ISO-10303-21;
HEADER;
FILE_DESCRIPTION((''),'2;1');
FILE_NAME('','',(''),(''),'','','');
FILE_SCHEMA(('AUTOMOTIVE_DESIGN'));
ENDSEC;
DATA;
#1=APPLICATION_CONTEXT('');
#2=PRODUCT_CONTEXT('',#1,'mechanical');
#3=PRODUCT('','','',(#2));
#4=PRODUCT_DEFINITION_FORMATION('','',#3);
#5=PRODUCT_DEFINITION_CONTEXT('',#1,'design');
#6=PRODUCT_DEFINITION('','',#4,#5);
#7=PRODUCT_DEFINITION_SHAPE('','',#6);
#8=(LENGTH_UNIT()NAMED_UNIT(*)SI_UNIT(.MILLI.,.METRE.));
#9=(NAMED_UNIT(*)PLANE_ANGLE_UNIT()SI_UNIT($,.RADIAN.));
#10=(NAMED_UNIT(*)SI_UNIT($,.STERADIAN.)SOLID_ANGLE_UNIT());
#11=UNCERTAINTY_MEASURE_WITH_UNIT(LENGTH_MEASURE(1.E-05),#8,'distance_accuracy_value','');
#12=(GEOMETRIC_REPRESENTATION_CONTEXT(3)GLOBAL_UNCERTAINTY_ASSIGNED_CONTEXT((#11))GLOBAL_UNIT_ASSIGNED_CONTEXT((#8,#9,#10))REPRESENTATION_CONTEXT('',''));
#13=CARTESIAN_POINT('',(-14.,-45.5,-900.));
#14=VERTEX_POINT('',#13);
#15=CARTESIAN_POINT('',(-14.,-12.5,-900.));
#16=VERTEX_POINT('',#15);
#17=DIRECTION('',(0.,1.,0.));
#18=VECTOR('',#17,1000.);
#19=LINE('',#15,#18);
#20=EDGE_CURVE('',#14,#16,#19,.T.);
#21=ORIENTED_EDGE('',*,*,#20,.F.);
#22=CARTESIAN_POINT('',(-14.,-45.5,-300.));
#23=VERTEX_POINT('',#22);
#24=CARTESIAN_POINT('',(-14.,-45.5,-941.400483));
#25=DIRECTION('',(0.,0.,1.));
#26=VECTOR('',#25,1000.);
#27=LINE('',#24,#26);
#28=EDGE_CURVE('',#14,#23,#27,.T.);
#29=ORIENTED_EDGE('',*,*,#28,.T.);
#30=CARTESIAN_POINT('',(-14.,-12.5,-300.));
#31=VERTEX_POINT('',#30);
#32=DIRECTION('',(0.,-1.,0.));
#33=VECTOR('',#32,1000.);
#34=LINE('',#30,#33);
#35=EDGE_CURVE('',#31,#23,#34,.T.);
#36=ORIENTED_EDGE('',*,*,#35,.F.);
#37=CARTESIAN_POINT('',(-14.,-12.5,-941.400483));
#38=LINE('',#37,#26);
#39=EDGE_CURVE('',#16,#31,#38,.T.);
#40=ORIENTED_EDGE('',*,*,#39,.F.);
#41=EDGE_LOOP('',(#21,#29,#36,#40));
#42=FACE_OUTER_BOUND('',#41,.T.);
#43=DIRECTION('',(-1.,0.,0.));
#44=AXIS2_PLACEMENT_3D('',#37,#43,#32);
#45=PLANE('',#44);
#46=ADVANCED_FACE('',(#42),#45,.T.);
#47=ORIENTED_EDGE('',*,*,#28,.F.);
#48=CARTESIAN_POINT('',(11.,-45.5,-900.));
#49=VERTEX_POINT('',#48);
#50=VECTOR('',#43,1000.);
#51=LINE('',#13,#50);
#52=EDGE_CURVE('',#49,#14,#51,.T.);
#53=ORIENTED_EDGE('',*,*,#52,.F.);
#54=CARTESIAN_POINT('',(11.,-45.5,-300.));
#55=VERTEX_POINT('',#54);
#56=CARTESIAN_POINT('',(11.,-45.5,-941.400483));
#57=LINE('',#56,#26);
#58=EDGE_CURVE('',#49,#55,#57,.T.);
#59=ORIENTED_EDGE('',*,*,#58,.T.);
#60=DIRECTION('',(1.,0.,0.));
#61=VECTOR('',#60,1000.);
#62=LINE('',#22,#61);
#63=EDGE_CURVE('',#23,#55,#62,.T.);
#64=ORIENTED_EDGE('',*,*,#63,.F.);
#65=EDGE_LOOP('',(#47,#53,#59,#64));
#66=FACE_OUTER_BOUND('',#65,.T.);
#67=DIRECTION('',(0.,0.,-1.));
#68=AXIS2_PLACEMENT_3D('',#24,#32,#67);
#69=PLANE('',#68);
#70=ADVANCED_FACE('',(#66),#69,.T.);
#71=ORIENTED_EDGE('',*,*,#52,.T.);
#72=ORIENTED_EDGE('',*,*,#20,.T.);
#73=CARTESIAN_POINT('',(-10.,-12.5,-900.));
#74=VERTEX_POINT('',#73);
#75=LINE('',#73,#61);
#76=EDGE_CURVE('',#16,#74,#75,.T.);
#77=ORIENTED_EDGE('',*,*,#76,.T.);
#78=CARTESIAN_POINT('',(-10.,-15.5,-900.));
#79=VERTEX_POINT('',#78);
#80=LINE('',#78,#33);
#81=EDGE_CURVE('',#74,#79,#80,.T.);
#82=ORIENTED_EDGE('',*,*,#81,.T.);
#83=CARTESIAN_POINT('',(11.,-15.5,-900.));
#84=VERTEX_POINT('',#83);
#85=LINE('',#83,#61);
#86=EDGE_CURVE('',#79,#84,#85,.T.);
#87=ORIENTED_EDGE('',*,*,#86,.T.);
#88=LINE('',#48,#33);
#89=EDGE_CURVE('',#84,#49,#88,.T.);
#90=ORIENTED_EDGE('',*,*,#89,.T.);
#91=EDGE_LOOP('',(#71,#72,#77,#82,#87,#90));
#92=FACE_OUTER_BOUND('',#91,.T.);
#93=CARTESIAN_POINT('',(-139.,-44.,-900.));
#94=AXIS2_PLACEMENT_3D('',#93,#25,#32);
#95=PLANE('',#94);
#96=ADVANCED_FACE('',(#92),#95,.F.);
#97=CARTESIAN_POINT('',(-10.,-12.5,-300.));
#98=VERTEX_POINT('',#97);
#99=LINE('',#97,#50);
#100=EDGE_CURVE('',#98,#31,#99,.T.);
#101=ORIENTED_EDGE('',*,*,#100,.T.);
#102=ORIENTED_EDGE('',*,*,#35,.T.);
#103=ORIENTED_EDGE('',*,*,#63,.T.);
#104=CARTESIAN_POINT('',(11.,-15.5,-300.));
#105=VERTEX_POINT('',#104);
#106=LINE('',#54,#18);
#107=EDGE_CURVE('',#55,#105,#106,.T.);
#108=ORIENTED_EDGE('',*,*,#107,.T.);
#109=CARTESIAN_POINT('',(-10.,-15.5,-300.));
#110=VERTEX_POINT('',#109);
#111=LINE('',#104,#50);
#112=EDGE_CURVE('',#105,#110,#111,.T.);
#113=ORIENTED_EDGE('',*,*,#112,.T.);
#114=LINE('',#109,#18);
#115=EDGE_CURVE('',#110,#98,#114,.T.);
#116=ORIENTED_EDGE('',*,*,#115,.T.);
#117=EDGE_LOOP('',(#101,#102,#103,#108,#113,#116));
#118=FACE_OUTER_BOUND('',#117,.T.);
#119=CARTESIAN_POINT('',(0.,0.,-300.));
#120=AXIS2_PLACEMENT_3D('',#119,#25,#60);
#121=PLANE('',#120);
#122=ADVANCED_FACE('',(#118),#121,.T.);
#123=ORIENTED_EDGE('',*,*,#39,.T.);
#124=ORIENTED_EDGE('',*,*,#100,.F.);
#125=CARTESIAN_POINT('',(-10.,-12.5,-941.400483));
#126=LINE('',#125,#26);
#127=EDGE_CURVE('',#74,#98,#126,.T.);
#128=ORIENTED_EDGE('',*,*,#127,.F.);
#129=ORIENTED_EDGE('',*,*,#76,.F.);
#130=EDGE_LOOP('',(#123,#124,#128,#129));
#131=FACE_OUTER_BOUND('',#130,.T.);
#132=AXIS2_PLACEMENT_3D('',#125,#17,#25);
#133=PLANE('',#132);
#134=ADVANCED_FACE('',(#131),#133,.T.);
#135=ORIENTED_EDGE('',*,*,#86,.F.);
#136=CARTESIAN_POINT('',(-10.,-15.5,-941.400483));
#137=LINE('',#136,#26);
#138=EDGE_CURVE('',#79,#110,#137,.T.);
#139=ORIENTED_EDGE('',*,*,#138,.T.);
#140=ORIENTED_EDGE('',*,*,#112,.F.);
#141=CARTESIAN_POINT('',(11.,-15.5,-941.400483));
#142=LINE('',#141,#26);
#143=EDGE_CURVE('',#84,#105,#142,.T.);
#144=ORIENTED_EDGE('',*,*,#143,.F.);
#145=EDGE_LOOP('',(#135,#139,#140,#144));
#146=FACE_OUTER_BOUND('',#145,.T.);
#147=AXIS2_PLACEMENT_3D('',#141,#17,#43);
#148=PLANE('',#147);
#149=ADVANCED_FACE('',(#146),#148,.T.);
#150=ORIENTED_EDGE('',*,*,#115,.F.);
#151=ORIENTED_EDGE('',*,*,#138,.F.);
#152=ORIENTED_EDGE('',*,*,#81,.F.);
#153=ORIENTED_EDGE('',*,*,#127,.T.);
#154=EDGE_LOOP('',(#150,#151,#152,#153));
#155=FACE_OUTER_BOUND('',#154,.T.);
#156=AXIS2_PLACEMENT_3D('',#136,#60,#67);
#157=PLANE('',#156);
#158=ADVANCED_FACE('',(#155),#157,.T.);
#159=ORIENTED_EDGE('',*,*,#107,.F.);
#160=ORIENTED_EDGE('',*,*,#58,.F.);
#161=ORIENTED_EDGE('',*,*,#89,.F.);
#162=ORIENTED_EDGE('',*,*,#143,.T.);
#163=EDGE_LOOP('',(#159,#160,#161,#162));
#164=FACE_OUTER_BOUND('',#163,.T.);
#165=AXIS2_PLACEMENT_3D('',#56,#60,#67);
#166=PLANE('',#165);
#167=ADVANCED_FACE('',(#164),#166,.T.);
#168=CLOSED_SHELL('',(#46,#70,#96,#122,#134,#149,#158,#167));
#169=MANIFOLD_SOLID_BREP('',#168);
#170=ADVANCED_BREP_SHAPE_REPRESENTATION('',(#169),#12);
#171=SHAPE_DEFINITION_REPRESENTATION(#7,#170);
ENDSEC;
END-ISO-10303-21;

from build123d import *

# Parameters (mm, degrees)
EXTRUDE_1_DEPTH = 600


with BuildPart() as part:
    # 草图1 → 凸台-拉伸1 (new body)
    with BuildSketch(Plane.XY.offset(-300)):
        Polygon((-10, -12.5), (-14, -12.5), (-14, -45.5), (11, -45.5), (11, -15.5), (-10, -15.5), align=None)
    extrude(amount=-EXTRUDE_1_DEPTH)


solid = part.part
